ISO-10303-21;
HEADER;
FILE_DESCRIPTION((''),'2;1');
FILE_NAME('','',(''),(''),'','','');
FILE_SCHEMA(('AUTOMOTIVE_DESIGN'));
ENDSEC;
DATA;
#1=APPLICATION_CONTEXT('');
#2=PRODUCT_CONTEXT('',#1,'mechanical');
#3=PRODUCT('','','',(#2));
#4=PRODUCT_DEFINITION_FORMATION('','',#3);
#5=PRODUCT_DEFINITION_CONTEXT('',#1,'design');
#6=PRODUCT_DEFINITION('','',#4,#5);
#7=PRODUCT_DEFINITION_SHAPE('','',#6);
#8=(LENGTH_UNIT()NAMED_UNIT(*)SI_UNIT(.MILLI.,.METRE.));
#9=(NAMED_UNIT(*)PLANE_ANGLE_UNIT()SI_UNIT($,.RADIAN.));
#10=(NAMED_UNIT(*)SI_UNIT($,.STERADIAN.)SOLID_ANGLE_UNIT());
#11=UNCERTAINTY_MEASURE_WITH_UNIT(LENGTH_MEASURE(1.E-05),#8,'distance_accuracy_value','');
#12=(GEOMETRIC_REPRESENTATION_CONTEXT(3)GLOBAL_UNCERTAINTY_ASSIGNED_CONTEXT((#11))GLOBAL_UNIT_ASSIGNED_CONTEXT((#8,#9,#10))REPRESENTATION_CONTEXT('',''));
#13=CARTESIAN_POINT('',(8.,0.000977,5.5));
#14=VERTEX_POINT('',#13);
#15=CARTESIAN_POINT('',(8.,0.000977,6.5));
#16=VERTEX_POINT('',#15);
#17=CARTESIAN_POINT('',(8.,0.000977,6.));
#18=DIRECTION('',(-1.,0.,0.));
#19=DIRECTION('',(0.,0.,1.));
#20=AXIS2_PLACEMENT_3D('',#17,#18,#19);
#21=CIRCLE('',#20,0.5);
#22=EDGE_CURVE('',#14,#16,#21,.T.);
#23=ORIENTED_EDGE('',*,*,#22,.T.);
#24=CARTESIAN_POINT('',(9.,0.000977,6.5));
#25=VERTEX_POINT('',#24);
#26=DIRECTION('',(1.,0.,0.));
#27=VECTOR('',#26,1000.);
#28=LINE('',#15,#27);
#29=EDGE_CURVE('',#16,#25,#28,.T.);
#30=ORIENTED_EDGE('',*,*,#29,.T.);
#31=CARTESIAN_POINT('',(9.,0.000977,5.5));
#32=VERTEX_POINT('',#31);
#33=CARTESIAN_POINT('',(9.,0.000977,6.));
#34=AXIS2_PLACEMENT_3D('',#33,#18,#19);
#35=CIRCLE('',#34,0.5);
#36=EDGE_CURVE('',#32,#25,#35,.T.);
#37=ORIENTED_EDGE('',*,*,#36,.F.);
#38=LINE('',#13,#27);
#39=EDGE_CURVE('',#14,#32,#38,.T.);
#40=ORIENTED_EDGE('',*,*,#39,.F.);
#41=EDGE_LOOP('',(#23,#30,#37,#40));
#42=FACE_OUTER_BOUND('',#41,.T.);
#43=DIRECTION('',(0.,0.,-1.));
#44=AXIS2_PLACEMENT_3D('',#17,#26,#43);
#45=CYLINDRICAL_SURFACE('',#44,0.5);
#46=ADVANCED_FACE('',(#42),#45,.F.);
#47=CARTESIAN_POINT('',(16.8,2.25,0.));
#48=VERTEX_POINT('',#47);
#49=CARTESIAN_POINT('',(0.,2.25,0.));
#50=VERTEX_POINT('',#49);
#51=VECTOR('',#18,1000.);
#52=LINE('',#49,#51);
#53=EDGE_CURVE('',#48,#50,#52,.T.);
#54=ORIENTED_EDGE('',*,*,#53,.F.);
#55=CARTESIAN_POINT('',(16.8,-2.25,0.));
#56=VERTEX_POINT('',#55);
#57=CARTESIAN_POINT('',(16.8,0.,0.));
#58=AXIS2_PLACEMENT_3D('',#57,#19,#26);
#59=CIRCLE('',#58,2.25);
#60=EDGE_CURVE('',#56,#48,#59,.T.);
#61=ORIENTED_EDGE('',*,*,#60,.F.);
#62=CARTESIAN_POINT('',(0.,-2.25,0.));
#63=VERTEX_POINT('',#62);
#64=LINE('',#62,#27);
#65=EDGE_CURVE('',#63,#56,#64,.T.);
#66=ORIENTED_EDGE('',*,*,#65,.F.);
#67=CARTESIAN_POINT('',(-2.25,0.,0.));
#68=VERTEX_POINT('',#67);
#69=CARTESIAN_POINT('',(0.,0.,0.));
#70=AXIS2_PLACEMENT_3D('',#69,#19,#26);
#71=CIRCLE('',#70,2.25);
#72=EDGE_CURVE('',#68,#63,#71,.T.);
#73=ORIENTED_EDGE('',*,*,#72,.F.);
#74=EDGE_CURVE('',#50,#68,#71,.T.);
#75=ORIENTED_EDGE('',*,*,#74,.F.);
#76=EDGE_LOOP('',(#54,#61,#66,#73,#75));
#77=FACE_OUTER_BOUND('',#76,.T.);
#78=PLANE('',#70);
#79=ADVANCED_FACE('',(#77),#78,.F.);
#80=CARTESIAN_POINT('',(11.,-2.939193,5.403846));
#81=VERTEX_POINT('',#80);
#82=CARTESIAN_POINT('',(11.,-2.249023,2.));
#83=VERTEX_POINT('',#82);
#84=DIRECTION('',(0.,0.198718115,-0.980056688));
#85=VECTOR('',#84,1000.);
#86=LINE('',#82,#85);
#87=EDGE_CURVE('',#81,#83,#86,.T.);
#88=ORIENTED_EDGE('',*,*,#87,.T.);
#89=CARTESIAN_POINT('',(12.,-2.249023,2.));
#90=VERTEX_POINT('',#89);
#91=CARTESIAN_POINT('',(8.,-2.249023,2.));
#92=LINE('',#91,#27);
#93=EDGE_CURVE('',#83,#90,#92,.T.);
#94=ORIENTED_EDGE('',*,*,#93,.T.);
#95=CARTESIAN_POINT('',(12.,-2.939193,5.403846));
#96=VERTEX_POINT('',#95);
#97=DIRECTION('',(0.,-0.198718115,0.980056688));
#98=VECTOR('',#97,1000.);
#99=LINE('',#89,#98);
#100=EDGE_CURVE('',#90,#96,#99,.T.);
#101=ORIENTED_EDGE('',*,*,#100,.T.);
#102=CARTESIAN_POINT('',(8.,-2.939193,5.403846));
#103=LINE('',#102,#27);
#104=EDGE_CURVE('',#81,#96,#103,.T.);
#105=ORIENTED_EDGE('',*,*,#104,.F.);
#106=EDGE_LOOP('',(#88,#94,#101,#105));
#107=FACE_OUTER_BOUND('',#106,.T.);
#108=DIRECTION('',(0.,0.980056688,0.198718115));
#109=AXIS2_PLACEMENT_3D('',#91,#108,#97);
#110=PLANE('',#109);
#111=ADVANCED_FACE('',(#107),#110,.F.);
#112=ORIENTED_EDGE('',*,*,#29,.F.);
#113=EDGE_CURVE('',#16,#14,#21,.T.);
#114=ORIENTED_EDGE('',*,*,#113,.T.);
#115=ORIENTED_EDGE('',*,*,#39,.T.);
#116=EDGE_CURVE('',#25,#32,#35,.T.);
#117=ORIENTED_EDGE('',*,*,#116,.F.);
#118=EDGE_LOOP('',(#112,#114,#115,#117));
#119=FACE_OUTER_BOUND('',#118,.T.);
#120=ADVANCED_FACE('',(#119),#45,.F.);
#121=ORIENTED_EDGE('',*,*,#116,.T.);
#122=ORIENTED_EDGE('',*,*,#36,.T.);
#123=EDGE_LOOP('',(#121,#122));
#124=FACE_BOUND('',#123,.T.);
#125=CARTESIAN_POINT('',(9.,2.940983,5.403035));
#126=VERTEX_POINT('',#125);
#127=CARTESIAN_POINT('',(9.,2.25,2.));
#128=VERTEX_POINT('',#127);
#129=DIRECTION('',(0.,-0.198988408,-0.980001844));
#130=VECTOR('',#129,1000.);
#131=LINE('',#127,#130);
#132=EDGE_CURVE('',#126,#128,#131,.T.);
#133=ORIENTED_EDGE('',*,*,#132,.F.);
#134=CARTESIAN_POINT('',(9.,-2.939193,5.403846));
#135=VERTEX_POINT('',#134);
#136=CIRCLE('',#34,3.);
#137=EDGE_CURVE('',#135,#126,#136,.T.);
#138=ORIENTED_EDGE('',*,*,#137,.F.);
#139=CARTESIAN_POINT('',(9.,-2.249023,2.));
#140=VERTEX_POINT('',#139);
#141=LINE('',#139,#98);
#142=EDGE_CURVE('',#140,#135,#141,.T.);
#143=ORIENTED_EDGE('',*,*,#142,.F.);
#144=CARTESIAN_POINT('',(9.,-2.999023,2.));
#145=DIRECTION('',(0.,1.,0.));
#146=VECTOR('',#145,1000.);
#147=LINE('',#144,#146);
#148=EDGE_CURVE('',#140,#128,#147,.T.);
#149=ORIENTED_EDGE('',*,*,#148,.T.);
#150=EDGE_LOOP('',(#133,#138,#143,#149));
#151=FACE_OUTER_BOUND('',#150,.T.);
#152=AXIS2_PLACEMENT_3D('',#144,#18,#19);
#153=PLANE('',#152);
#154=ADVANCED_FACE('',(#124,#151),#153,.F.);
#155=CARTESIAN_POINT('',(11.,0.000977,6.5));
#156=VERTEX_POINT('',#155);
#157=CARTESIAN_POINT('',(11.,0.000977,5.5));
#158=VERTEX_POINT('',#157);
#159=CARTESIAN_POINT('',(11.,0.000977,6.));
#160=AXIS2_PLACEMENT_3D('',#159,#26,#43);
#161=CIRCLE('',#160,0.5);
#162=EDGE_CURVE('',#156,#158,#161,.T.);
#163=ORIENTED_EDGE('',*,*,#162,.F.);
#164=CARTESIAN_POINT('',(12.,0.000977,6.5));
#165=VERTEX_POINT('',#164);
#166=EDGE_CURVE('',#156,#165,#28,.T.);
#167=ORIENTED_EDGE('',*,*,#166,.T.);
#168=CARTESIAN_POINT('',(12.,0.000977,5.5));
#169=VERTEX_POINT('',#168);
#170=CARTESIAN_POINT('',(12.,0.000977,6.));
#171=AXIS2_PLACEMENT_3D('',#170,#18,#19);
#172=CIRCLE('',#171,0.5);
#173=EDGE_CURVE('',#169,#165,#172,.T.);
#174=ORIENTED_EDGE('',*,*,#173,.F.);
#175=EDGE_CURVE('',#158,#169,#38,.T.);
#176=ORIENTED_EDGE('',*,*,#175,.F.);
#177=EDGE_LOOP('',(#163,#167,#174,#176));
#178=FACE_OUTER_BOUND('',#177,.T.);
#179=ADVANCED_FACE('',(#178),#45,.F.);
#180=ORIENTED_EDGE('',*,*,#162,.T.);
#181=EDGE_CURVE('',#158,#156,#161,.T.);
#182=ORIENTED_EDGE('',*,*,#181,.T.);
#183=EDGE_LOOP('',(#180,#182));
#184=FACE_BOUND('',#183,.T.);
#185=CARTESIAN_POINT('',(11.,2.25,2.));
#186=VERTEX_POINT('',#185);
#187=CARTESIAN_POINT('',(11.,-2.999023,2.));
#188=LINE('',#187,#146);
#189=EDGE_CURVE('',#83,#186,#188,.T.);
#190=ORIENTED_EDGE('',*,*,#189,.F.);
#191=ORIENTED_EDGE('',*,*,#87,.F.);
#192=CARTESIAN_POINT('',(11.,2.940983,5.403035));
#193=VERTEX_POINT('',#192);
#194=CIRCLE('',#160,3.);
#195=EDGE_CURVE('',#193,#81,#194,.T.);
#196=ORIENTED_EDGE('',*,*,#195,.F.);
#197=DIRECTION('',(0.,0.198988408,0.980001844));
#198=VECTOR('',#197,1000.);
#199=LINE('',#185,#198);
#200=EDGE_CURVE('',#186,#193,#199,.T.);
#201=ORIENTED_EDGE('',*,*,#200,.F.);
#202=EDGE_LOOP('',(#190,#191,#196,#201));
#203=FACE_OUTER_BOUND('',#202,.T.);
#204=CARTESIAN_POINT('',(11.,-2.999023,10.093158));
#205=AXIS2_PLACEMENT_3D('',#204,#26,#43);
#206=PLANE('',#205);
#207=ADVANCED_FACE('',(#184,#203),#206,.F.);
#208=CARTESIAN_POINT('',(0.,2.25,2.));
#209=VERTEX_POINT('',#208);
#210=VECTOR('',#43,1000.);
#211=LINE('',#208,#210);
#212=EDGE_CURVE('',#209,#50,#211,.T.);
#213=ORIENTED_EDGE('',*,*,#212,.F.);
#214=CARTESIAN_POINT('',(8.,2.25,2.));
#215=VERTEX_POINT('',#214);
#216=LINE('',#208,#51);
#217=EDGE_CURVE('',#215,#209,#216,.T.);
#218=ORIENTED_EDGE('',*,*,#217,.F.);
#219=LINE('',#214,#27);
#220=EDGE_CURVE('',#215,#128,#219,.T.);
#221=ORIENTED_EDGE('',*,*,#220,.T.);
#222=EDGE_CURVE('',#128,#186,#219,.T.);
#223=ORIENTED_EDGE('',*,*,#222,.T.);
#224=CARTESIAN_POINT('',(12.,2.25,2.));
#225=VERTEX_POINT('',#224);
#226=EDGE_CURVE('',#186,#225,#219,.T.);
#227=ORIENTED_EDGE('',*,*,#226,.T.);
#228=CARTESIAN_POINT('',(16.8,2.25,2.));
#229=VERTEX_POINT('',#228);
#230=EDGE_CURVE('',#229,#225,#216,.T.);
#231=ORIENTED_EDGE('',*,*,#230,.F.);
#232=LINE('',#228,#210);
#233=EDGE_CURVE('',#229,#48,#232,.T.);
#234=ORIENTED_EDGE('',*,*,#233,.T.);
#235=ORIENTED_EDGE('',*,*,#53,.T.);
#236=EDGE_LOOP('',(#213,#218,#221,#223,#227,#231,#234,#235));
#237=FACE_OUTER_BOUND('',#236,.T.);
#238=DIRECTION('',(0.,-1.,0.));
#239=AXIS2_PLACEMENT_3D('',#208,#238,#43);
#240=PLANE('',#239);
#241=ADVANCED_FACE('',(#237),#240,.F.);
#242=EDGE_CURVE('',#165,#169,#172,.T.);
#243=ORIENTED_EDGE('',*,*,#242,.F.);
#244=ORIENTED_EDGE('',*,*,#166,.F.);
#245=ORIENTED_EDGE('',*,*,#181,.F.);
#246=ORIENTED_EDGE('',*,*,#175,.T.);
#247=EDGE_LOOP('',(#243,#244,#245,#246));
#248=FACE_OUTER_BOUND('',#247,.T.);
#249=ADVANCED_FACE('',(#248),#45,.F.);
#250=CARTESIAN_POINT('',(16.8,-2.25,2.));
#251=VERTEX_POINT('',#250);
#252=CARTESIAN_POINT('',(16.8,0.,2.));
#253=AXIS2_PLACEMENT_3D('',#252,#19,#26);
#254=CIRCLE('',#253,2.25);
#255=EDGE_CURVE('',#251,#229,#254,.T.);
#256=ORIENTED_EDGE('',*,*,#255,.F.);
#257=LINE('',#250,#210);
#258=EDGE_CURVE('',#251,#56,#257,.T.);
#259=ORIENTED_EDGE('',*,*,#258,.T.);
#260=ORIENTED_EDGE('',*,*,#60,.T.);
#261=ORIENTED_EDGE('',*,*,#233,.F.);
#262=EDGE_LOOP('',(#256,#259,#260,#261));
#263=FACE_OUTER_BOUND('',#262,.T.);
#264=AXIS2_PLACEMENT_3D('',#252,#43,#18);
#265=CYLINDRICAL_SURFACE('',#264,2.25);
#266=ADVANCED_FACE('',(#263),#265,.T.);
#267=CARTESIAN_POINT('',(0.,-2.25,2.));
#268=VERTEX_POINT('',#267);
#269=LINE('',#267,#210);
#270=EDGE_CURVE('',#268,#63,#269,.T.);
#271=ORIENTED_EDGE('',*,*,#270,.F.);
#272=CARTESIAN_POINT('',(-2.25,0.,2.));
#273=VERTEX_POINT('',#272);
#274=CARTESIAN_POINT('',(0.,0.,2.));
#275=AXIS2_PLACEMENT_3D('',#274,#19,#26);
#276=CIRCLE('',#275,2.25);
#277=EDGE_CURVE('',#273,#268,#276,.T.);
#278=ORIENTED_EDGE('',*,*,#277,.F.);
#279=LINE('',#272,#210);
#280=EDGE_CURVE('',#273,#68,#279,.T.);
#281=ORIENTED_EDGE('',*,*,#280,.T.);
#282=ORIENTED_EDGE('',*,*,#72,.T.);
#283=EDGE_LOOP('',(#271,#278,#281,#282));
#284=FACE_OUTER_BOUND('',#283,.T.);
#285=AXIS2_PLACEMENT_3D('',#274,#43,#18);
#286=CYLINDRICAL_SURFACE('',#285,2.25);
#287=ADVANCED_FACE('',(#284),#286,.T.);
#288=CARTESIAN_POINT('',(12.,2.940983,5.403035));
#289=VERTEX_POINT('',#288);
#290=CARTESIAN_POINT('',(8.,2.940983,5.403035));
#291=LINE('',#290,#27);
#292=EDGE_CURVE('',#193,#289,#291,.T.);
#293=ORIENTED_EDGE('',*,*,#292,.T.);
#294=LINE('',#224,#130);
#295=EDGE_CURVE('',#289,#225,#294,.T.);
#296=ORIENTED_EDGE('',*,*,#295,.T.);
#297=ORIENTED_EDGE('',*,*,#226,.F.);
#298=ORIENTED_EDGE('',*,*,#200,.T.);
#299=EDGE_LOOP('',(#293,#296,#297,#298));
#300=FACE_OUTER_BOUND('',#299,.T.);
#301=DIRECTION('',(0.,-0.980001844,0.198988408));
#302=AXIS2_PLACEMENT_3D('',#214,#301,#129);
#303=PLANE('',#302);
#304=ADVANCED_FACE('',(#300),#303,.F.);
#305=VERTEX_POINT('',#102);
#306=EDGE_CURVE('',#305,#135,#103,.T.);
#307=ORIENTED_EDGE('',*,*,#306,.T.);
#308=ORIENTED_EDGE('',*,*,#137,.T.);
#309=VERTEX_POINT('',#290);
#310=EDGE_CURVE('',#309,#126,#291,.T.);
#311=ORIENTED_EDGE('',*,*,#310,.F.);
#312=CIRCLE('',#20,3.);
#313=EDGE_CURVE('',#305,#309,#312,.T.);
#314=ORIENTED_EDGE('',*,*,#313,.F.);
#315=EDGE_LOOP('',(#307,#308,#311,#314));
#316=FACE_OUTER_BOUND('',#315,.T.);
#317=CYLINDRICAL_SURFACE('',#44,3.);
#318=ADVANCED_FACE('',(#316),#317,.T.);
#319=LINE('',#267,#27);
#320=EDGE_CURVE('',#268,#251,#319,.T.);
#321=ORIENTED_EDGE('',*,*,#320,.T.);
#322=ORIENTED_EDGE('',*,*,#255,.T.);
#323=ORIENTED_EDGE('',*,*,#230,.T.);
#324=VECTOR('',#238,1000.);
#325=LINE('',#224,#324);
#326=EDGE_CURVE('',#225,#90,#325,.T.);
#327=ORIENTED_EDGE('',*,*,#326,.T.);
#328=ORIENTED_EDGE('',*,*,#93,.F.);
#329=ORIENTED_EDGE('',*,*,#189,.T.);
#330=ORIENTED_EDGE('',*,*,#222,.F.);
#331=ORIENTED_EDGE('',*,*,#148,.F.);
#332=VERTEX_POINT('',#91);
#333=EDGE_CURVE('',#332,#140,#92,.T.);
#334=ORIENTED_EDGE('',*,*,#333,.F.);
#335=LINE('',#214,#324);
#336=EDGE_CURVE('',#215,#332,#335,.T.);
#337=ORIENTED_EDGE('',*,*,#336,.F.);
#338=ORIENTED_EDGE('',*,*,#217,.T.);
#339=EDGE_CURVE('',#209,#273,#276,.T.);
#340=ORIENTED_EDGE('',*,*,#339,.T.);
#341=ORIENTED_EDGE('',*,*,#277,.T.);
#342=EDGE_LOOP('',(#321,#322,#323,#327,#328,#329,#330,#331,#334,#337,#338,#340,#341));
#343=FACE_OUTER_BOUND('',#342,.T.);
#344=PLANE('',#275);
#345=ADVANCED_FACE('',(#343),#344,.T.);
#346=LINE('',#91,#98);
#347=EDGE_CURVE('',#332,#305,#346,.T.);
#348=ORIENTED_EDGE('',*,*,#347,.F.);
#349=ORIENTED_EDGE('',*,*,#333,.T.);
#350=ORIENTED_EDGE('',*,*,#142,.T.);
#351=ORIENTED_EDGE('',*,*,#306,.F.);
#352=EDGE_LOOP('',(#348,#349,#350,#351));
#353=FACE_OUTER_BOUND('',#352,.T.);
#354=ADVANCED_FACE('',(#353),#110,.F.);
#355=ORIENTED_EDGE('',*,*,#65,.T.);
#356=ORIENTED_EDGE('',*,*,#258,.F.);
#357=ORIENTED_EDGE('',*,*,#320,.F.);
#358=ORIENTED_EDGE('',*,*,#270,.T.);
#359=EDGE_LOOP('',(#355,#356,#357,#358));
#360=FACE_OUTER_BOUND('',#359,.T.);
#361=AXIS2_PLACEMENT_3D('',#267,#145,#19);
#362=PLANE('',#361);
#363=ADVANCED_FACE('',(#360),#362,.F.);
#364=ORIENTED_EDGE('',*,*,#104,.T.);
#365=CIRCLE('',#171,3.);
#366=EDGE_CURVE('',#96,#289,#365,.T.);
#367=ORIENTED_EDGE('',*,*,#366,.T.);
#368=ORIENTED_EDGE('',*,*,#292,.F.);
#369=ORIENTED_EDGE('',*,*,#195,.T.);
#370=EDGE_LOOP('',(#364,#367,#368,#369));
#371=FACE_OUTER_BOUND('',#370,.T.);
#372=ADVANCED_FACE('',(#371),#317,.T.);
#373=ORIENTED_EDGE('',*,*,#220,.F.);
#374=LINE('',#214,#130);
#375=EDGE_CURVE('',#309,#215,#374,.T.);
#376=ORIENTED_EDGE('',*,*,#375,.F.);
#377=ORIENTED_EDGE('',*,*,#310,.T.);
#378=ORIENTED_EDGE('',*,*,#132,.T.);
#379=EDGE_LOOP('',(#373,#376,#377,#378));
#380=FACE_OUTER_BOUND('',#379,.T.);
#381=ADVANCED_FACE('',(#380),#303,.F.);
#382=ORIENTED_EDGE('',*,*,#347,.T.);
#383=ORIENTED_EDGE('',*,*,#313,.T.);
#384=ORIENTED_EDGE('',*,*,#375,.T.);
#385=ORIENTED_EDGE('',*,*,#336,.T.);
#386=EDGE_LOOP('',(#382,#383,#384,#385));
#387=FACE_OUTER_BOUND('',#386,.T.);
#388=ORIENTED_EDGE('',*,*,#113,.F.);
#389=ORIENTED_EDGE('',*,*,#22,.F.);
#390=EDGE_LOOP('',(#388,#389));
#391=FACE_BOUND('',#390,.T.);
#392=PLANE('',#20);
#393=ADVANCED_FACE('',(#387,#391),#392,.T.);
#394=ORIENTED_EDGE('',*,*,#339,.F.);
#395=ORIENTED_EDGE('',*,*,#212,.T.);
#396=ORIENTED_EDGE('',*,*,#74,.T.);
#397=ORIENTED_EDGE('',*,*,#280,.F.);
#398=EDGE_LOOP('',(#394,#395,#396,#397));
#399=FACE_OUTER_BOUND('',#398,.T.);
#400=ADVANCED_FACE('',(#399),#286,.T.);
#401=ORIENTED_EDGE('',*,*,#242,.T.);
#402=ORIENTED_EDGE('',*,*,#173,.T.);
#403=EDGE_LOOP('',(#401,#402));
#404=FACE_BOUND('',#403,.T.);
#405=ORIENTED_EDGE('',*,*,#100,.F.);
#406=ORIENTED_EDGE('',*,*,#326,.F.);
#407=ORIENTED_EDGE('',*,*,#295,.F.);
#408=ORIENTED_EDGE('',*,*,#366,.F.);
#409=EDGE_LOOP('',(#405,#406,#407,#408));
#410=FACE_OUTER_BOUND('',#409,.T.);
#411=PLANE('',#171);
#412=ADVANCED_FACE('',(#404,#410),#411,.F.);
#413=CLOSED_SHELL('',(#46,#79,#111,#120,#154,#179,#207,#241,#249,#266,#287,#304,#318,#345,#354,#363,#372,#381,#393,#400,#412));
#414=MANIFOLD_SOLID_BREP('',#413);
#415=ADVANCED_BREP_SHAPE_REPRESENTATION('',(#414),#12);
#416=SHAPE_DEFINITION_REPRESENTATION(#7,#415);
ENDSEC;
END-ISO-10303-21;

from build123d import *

# Parameters (mm, degrees)
BOSS_EXTRUDE_1_DEPTH     = 2
SKETCH_3_R               = 0.5
BOSS_EXTRUDE_2_DEPTH     = 4
CUT_EXTRUDE_1_DEPTH      = 22.281643835
CUT_EXTRUDE_1_DEPTH_BACK = 22.281643835
SKETCH_4_W               = 2
SKETCH_4_H               = 8.093157612


with BuildPart() as part:
    # Sketch 1 → Boss-Extrude 1 (new body)
    with BuildSketch(Plane.XY):
        with BuildLine():
            Line((0, 2.25), (16.8, 2.25))
            ThreePointArc((16.8, 2.25), (19.05, 0), (16.8, -2.25))
            Line((16.8, -2.25), (0, -2.25))
            ThreePointArc((0, -2.25), (-2.25, 0), (0, 2.25))
        make_face()
    extrude(amount=BOSS_EXTRUDE_1_DEPTH)

    # Sketch 3 → Boss-Extrude 2 (add)
    with BuildSketch(Plane.ZY.offset(-12)):
        with BuildLine():
            Line((2, 2.25), (2, -2.249022682))
            Line((2, -2.249022682), (5.403845626, -2.939192745))
            ThreePointArc((5.403845626, -2.939192745), (8.999999942, 0.001391019), (5.403034747, 2.940982849))
            Line((5.403034747, 2.940982849), (2, 2.25))
        make_face()
        with Locations((5.99999997, 0.000977318)):
            Circle(SKETCH_3_R, mode=Mode.SUBTRACT)
    extrude(amount=BOSS_EXTRUDE_2_DEPTH)

    # Sketch 4 → Cut-Extrude 1 (cut, two sides: drawn at the far end of the back side and taken through both)
    with BuildSketch(Plane(origin=(0, 0, 0), x_dir=(1, 0, 0), z_dir=(0, 1, 0)).offset(-CUT_EXTRUDE_1_DEPTH_BACK)):
        with Locations((10, -6.046578806)):
            Rectangle(SKETCH_4_W, SKETCH_4_H)
    extrude(amount=CUT_EXTRUDE_1_DEPTH + CUT_EXTRUDE_1_DEPTH_BACK, mode=Mode.SUBTRACT)


solid = part.part
